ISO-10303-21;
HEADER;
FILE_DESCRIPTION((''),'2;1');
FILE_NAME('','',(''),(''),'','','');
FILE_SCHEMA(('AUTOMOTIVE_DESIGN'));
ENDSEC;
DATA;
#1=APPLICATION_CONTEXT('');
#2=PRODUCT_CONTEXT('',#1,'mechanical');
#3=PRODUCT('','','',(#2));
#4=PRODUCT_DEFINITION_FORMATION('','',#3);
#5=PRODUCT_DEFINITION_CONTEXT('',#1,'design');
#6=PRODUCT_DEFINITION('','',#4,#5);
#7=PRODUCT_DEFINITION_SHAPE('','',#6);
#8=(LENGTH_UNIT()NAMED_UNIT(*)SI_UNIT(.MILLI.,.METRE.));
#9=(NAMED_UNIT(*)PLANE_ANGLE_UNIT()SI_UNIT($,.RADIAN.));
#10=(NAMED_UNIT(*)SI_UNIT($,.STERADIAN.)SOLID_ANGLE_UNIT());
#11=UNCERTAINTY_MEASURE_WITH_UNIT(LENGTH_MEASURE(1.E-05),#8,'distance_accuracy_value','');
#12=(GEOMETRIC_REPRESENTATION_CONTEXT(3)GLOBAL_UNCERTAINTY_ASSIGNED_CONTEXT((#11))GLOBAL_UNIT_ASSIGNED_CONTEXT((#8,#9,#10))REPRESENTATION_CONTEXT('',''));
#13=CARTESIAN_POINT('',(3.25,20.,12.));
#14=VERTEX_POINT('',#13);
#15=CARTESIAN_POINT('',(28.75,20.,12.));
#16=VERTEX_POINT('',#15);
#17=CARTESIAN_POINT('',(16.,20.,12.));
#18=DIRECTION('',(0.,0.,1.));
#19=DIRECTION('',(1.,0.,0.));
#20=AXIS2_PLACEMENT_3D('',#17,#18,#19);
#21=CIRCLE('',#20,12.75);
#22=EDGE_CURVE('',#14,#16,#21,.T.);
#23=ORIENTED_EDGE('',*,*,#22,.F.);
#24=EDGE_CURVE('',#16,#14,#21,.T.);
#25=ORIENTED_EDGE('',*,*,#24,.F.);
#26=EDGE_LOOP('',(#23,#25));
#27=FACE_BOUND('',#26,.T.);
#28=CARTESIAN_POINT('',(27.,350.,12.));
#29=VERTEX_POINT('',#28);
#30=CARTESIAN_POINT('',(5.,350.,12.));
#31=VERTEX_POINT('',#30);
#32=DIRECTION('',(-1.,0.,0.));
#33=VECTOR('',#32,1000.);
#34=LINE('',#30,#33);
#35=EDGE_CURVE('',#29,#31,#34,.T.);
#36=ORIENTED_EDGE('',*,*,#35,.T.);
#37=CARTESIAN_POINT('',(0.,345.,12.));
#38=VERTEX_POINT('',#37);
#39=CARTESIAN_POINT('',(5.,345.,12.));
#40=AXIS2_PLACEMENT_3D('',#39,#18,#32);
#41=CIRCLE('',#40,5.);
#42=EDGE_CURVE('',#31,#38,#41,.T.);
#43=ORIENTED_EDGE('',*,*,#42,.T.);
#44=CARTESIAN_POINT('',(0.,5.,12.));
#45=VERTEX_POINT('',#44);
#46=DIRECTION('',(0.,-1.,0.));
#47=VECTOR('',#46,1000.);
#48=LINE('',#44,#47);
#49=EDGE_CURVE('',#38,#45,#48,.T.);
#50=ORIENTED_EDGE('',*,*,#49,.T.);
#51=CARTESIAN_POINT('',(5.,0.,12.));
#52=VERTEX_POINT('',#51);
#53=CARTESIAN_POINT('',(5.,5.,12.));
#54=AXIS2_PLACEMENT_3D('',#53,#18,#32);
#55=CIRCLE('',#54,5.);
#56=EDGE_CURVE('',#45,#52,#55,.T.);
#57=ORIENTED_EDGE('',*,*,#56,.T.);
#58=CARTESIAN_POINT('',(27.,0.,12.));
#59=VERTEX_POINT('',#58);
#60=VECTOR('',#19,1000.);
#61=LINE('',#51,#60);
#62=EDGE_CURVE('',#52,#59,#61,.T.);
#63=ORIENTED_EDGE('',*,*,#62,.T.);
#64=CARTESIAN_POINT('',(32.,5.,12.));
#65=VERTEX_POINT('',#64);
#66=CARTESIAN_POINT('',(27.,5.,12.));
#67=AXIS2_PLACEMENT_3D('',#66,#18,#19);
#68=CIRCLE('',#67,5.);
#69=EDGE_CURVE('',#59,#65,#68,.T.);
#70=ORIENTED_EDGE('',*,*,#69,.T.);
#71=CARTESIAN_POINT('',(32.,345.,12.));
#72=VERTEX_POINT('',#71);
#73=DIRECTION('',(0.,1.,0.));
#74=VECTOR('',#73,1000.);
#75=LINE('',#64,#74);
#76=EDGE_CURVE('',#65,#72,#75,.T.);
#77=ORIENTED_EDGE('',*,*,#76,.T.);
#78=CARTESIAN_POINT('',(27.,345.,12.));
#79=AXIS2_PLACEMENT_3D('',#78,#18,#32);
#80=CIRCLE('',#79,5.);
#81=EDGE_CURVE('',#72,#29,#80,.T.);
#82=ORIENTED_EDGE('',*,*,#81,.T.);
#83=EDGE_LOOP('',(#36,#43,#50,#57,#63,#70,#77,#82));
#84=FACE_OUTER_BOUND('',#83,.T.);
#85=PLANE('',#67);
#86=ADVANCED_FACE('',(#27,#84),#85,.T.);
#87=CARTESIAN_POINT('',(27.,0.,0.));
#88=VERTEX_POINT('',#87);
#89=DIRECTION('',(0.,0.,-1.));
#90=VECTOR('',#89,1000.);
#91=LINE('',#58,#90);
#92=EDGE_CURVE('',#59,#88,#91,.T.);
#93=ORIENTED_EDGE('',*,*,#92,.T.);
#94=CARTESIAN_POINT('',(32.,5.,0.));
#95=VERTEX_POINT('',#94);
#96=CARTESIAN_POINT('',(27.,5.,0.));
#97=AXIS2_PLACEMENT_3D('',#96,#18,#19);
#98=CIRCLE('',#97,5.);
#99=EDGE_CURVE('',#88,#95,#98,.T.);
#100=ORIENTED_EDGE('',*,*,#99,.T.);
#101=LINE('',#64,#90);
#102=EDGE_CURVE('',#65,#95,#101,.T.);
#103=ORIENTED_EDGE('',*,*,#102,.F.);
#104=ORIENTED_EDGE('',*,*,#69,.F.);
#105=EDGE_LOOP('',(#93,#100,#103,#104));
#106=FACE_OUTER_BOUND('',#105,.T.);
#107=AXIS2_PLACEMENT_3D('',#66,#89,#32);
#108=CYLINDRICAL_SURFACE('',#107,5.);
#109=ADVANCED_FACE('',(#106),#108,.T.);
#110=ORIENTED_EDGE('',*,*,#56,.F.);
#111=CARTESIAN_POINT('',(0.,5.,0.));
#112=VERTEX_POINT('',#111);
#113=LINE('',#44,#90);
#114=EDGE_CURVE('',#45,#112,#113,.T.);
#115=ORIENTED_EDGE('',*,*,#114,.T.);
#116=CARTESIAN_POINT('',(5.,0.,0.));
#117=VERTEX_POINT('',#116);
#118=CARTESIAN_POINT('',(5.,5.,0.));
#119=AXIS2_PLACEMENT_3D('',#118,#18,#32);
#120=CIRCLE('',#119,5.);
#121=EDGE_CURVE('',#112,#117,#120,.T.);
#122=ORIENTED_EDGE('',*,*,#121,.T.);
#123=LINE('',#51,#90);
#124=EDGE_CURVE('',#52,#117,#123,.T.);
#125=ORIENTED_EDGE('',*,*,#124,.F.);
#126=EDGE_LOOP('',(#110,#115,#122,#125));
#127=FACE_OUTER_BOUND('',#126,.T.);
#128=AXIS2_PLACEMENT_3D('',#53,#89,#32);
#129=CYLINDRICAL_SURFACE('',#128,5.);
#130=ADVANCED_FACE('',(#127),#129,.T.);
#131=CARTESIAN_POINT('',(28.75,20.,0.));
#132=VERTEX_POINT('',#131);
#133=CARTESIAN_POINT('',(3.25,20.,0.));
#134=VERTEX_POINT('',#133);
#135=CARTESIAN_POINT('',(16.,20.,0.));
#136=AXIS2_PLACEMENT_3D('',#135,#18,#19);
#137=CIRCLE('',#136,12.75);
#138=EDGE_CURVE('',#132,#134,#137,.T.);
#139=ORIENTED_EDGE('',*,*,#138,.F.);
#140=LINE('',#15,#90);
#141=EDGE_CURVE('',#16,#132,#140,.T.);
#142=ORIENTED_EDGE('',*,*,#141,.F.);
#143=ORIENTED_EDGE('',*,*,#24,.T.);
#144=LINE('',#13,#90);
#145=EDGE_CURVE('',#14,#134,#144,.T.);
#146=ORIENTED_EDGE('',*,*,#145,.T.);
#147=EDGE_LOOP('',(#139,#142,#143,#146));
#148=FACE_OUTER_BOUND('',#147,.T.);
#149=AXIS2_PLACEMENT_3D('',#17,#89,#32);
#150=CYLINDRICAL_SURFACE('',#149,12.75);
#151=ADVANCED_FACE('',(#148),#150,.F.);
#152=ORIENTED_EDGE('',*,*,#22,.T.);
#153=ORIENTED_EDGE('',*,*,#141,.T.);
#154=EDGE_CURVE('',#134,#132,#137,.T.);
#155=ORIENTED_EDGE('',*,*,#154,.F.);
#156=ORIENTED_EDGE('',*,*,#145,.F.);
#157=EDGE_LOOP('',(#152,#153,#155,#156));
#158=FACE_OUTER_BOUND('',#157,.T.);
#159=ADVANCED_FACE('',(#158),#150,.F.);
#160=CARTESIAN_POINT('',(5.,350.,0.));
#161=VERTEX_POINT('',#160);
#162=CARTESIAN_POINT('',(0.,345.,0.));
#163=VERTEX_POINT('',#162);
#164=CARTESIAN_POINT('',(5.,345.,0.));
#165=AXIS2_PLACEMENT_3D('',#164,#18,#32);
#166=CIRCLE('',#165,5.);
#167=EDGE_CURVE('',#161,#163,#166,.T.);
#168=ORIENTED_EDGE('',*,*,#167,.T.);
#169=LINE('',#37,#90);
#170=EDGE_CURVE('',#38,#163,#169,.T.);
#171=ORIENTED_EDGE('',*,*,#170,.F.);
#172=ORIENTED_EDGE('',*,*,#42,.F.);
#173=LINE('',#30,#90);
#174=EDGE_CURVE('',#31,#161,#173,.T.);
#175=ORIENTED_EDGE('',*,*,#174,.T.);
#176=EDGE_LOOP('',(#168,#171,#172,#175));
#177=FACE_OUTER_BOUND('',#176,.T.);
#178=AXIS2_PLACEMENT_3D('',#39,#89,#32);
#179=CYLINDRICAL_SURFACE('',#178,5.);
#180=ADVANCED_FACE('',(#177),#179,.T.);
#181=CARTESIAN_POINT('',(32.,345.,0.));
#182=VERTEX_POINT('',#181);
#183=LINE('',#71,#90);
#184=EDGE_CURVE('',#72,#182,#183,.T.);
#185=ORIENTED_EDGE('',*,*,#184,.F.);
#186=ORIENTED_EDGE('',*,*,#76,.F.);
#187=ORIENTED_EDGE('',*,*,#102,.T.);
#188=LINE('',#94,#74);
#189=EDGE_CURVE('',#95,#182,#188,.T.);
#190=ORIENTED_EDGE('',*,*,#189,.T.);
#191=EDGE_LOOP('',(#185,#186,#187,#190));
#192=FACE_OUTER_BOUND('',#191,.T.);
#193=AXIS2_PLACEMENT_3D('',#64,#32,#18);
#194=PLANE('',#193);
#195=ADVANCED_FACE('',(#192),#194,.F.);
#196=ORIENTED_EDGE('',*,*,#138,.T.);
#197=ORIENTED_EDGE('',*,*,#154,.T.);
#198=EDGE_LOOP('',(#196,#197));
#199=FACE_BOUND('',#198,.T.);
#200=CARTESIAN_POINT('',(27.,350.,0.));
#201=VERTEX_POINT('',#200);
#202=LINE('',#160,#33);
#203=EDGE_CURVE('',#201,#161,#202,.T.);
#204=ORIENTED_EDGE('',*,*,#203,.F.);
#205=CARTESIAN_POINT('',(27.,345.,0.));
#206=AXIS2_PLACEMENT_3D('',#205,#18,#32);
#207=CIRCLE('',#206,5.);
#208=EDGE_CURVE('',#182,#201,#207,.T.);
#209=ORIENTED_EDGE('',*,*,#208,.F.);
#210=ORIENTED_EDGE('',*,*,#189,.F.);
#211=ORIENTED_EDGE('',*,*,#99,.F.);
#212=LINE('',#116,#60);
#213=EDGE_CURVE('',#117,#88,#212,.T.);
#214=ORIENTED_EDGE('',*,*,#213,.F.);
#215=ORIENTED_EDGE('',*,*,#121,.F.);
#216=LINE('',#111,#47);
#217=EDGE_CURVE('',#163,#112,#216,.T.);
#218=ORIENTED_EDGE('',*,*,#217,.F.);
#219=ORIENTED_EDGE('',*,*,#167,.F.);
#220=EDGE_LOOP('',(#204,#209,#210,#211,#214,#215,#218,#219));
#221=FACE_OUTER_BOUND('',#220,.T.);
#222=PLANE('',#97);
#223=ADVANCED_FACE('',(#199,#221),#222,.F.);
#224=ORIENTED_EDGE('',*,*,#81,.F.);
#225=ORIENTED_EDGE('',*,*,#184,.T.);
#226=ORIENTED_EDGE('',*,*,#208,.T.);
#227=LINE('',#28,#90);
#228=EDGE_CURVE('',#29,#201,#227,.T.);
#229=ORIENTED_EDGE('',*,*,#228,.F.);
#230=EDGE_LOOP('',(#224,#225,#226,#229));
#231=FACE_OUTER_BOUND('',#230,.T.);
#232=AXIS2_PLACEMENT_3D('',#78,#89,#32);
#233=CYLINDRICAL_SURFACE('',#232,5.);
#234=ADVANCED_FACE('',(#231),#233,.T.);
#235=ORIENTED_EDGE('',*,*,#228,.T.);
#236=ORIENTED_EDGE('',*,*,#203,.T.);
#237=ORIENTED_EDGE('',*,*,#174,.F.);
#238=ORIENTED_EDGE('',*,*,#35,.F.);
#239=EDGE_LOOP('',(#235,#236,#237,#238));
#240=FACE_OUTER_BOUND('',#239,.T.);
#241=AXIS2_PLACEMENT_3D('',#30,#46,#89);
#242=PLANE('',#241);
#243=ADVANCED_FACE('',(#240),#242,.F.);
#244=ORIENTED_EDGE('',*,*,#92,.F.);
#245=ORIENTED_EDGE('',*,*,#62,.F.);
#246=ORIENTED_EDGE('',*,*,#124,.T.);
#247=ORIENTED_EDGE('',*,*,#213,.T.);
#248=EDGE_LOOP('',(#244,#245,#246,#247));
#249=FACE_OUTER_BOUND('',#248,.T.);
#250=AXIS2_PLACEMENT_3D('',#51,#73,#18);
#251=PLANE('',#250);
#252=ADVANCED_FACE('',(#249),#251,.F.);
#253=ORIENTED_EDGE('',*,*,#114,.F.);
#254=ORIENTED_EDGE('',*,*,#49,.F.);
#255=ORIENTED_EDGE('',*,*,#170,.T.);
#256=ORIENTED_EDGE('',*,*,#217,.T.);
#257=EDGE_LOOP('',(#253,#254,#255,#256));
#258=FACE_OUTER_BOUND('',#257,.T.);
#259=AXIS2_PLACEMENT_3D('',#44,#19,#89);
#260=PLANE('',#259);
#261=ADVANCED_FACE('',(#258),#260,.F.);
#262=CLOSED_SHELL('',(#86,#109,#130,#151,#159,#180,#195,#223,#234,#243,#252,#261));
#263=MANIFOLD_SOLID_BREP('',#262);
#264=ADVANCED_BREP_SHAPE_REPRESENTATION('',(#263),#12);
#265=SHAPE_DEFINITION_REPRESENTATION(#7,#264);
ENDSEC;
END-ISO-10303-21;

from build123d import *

# Parameters (mm, degrees)
SKETCH1_R           = 12.75
BOSS_EXTRUDE1_DEPTH = 12


with BuildPart() as part:
    # Sketch1 → Boss-Extrude1 (new body)
    with BuildSketch(Plane.XY):
        with BuildLine():
            Line((5, 0), (27, 0))
            ThreePointArc((27, 0), (30.535533906, 1.464466094), (32, 5))
            Line((32, 5), (32, 345))
            ThreePointArc((32, 345), (30.535533906, 348.535533906), (27, 350))
            Line((27, 350), (5, 350))
            ThreePointArc((5, 350), (1.464466094, 348.535533906), (0, 345))
            Line((0, 345), (0, 5))
            ThreePointArc((0, 5), (1.464466094, 1.464466094), (5, 0))
        make_face()
        with Locations((16, 20)):
            Circle(SKETCH1_R, mode=Mode.SUBTRACT)
    extrude(amount=BOSS_EXTRUDE1_DEPTH)


solid = part.part
